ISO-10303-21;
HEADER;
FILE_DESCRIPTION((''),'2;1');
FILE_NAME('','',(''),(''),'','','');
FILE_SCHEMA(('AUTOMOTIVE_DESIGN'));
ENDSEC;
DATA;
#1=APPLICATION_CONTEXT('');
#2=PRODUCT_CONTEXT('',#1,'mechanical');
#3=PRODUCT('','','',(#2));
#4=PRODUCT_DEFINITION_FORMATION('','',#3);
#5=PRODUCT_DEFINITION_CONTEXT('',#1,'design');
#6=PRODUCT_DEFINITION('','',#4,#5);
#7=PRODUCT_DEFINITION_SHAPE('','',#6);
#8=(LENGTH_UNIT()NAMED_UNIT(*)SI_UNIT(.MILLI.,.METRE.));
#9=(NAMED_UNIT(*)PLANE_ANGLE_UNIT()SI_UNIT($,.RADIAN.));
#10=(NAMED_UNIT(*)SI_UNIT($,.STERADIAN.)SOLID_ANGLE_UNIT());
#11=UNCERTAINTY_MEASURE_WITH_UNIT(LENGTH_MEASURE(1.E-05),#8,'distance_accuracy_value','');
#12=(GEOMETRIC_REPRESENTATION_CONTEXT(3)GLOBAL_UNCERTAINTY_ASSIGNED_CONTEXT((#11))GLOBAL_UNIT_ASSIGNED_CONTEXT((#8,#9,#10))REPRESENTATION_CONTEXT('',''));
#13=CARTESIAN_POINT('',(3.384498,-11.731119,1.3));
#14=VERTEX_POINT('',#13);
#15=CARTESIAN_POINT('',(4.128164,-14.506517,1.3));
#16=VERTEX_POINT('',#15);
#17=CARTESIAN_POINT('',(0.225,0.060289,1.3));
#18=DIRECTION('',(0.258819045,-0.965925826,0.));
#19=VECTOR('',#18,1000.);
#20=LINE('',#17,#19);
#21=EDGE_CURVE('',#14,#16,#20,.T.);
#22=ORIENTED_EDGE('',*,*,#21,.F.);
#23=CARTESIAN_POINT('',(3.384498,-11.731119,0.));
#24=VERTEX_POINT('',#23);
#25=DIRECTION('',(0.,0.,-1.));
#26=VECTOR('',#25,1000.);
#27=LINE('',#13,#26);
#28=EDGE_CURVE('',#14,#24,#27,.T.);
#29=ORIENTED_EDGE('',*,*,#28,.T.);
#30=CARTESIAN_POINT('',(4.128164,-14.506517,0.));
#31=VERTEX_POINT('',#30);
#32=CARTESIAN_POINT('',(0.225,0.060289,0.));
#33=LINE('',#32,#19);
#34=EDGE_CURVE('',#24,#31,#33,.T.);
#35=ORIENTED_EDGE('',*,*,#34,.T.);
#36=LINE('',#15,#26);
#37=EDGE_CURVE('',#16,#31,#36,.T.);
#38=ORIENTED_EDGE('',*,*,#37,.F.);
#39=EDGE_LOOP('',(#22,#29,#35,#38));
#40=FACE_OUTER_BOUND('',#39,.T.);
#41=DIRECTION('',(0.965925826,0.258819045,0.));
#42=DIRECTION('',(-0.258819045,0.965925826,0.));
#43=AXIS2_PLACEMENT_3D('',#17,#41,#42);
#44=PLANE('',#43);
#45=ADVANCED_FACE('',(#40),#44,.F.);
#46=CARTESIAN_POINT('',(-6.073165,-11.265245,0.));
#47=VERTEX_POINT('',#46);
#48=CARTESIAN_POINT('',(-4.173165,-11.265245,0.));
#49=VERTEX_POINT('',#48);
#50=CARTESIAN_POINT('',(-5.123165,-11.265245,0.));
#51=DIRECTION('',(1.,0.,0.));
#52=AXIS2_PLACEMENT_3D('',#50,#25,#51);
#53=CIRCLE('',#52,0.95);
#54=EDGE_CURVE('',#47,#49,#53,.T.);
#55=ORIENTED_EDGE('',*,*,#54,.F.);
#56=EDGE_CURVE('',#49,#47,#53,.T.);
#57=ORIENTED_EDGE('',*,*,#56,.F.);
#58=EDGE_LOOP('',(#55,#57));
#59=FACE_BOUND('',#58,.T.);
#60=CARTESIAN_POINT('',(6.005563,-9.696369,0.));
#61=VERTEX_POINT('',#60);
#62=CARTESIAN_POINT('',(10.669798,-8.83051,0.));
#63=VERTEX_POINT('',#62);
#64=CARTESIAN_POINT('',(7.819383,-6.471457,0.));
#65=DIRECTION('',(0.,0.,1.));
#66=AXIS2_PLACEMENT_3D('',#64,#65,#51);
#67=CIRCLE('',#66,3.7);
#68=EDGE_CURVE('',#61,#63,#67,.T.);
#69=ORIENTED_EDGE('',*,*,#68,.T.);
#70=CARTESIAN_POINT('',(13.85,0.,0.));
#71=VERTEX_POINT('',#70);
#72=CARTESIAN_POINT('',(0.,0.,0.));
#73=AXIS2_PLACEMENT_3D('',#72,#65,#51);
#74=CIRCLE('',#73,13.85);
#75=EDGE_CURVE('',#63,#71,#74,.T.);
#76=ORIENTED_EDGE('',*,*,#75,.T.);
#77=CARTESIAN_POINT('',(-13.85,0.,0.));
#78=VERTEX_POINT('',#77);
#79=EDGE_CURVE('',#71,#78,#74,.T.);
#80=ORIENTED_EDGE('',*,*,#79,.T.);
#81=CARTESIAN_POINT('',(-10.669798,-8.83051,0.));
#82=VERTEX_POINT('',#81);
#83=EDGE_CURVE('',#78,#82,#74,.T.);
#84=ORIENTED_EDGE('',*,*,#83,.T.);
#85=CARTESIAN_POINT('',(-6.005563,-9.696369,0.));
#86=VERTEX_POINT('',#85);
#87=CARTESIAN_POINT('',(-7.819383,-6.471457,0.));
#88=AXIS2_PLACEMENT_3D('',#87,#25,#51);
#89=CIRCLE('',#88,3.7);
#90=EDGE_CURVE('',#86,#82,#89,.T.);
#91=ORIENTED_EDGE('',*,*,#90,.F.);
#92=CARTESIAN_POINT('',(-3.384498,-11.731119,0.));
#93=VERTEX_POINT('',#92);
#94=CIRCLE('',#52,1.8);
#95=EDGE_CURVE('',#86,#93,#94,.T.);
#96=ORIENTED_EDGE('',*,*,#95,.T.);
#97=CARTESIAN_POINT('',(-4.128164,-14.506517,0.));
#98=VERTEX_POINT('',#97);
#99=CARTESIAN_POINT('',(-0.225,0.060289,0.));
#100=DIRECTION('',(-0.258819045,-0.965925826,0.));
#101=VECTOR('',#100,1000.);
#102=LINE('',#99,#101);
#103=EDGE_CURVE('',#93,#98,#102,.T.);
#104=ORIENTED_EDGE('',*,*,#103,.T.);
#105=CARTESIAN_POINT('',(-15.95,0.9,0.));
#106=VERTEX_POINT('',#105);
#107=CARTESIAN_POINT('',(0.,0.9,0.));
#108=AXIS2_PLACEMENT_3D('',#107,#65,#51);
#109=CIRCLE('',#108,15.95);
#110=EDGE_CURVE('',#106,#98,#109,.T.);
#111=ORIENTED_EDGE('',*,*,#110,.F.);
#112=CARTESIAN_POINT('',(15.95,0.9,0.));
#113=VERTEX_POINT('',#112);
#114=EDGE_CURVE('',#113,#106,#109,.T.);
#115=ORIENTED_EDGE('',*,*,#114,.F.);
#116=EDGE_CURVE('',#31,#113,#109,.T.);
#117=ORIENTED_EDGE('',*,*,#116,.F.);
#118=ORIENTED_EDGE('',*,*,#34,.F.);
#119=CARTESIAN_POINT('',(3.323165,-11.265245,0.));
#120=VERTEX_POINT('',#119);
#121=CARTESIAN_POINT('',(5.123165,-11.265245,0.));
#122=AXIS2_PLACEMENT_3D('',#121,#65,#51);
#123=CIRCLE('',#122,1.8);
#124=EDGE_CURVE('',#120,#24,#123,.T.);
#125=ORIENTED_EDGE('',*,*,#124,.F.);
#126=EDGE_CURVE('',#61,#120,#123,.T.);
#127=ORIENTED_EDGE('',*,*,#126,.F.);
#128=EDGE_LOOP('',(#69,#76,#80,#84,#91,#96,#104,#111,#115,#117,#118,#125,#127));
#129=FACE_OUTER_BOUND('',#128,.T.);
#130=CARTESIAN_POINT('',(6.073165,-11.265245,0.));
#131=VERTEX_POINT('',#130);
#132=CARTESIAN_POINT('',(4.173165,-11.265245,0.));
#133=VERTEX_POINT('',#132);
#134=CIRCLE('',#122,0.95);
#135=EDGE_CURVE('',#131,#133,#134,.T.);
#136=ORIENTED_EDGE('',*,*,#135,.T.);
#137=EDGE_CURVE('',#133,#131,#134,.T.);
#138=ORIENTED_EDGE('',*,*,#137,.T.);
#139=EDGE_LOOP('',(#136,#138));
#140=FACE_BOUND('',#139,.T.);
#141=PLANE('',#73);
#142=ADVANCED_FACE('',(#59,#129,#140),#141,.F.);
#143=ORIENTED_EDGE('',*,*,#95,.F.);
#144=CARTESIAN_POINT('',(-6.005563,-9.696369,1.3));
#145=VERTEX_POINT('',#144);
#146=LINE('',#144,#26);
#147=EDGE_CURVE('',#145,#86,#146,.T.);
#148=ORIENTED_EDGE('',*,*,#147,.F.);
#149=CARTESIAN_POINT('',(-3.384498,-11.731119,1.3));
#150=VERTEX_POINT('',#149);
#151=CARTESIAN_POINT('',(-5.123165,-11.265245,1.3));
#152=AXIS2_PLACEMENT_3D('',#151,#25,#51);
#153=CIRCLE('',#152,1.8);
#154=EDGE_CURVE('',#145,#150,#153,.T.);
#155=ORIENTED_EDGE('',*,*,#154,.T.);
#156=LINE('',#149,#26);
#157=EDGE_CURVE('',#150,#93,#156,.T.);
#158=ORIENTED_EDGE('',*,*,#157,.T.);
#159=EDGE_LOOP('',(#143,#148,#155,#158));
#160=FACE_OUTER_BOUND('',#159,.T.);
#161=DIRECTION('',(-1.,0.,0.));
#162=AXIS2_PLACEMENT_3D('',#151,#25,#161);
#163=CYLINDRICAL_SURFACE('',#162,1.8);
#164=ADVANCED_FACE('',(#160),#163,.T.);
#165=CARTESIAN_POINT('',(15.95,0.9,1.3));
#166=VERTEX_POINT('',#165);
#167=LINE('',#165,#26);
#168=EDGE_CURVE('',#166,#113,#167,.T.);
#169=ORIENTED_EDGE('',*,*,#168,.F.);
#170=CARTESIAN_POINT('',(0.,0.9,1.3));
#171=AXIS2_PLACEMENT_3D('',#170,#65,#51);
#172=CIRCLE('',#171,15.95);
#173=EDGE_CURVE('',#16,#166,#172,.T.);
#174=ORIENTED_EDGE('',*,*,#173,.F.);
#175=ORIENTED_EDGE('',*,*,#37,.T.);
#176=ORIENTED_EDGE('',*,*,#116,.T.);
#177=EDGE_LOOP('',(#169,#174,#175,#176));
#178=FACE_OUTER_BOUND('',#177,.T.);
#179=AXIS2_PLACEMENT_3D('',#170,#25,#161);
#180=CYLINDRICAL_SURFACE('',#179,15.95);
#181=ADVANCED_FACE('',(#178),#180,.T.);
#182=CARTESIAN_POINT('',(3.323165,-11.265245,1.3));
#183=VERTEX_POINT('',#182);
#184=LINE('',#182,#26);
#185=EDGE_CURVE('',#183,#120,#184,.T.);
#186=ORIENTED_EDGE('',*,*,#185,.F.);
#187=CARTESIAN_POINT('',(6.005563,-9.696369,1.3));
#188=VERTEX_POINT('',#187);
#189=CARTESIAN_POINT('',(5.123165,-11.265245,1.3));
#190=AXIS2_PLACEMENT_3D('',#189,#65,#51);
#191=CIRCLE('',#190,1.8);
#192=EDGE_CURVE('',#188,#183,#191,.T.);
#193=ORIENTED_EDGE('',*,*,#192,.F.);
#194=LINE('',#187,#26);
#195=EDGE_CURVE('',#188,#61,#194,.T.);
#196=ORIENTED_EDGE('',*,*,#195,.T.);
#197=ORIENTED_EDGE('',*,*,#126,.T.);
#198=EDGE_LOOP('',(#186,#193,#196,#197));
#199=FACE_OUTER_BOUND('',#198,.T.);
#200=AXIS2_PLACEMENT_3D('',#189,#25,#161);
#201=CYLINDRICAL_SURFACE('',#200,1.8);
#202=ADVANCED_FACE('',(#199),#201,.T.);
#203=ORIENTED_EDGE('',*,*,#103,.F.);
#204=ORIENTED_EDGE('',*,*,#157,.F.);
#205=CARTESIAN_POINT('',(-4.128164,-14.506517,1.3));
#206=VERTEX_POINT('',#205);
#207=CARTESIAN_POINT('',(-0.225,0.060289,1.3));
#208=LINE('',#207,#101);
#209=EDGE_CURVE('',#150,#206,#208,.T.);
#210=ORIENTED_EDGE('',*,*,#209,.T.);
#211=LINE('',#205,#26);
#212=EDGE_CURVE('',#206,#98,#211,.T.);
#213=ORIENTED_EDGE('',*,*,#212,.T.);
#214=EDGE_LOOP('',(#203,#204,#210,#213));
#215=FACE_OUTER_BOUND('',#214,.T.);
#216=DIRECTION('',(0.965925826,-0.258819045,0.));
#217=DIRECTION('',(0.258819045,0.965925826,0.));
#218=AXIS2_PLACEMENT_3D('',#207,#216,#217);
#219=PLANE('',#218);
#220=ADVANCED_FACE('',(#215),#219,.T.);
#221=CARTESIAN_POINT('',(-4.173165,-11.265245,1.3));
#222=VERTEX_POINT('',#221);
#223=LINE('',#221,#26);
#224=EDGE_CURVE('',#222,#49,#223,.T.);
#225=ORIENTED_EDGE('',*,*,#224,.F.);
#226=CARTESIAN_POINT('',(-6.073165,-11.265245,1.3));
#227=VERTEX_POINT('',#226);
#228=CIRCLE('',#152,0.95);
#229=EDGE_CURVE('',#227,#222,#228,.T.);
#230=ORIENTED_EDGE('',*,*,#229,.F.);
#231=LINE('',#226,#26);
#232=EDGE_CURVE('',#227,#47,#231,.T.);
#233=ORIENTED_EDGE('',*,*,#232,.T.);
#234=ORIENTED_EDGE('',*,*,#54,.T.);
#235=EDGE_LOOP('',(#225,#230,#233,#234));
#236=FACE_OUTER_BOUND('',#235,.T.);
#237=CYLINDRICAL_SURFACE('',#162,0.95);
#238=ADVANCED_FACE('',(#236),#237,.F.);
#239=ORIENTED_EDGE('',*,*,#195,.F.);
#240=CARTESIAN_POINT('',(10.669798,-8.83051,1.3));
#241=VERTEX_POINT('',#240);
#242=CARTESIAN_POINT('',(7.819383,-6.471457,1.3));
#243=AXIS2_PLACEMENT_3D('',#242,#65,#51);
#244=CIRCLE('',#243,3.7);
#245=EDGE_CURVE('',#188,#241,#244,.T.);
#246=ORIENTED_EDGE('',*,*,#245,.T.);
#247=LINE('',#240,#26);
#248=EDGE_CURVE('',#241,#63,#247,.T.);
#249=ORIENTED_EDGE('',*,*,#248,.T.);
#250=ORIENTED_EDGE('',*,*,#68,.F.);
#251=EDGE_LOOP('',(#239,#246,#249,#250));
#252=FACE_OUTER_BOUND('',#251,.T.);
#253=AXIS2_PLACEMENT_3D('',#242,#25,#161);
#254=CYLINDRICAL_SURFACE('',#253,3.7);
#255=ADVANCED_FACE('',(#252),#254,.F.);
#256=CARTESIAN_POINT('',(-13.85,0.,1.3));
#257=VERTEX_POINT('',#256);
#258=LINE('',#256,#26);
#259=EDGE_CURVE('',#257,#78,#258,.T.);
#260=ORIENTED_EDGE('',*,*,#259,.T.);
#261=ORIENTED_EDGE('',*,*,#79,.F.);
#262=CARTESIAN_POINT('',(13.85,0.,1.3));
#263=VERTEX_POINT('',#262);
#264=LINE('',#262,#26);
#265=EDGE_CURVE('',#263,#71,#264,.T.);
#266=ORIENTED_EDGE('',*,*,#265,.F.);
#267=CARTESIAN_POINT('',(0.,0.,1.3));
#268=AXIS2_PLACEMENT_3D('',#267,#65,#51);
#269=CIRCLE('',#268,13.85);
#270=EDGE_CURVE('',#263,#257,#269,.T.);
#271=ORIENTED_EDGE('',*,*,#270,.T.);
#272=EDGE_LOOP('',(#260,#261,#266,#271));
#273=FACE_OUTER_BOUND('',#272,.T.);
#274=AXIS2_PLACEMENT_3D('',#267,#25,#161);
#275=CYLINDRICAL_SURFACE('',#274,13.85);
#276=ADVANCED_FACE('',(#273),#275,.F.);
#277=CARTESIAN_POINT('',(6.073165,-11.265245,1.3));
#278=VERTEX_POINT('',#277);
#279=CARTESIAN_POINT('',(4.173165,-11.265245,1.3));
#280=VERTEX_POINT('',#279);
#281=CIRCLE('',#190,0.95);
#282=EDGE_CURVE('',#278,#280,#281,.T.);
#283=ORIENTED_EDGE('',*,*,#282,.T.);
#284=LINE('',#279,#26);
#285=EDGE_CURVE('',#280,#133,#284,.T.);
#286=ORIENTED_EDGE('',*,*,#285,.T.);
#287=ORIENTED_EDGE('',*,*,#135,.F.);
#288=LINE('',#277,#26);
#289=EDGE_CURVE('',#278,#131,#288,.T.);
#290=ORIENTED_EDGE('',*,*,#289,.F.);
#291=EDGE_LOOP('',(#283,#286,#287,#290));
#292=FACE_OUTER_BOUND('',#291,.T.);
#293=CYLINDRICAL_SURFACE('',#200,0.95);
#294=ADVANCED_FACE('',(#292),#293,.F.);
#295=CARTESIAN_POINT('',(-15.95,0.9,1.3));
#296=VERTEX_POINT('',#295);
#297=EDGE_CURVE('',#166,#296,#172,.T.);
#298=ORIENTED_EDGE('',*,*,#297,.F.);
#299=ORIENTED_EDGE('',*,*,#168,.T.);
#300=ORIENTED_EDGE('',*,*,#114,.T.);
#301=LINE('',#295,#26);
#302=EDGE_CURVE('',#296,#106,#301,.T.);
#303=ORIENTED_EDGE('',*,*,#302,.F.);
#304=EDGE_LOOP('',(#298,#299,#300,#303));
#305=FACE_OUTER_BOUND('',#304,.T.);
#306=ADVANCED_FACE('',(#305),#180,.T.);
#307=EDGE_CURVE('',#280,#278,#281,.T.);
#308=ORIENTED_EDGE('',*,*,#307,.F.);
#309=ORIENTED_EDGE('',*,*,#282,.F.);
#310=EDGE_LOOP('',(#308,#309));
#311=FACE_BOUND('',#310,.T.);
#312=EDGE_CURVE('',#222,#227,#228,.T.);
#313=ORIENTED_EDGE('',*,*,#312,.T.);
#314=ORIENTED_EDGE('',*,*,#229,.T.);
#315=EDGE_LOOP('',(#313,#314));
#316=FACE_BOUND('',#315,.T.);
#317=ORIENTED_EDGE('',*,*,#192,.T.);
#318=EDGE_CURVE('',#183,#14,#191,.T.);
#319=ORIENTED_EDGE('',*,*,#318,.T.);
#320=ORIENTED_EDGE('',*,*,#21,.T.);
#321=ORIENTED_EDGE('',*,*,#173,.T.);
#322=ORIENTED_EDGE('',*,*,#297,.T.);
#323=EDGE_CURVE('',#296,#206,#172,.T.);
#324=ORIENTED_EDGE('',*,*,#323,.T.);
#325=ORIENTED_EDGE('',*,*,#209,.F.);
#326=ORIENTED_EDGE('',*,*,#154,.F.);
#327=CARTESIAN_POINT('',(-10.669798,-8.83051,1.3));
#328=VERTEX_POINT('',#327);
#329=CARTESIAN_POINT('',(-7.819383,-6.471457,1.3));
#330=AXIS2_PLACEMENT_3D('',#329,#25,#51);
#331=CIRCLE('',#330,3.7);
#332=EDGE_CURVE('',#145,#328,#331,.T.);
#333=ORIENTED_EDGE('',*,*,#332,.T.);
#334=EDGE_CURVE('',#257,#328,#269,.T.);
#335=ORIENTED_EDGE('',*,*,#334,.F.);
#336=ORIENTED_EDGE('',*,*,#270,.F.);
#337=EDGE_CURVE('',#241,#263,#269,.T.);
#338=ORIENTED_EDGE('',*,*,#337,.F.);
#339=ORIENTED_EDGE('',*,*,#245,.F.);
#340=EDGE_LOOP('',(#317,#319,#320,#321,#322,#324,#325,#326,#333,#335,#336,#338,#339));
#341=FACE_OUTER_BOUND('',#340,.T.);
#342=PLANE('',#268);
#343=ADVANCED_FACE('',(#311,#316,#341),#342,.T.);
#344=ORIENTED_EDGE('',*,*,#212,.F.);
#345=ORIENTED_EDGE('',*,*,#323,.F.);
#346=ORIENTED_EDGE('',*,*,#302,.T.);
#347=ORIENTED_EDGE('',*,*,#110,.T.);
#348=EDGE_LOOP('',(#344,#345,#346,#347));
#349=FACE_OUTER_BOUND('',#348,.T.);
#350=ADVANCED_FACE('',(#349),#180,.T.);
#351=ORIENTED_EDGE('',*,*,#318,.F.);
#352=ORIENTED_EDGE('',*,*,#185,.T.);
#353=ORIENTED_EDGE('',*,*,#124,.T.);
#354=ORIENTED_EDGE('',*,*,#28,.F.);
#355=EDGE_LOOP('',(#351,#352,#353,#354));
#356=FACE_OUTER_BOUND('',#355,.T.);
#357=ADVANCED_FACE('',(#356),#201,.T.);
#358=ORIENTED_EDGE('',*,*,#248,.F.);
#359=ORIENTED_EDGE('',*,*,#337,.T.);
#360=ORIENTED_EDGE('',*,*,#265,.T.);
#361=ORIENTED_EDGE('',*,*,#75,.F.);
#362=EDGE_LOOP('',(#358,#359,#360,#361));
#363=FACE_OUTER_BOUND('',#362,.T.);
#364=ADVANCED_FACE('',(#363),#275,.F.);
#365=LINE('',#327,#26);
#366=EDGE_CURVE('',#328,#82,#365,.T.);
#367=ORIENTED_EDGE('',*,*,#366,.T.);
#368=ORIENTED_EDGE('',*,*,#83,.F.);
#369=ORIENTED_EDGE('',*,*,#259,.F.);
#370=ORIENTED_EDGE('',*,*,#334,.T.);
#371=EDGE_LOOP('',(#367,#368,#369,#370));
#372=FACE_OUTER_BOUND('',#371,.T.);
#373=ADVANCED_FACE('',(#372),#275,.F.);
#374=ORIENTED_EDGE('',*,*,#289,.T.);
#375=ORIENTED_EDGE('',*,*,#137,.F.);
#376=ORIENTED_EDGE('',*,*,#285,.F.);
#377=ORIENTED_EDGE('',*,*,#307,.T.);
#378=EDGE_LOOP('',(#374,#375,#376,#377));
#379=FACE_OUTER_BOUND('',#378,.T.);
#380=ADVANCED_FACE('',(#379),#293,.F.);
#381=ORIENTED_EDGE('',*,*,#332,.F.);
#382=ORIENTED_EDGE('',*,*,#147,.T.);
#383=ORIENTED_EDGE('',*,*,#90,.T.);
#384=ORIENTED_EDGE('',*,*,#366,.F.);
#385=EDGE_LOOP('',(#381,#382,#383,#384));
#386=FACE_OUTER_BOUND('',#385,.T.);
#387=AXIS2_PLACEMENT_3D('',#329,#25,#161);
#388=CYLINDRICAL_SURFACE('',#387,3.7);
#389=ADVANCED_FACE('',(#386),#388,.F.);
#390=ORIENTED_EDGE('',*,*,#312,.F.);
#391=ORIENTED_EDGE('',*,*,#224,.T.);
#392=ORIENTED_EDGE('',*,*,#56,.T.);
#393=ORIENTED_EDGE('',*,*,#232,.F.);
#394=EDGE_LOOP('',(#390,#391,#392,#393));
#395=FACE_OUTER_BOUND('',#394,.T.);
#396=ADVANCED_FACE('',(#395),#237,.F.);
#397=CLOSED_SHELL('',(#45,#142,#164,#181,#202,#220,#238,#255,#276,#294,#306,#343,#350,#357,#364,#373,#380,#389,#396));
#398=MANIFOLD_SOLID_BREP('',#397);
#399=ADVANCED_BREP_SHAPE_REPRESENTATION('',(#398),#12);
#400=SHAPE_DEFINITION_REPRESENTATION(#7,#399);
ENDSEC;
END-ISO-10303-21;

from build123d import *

# Parameters (mm, degrees)
SKETCH1_R           = 0.95
BOSS_EXTRUDE1_DEPTH = 1.3


with BuildPart() as part:
    # Sketch1 → Boss-Extrude1 (new body)
    with BuildSketch(Plane.XY):
        with BuildLine():
            ThreePointArc((-6.005563392, -9.696368719), (-4.019375294, -9.84339787), (-3.384498187, -11.731119191))
            Line((-3.384498187, -11.731119191), (-4.128163769, -14.506516929))
            ThreePointArc((-4.128163769, -14.506516929), (0, 16.85), (4.128163769, -14.506516929))
            Line((4.128163769, -14.506516929), (3.384498187, -11.731119191))
            ThreePointArc((3.384498187, -11.731119191), (4.019375294, -9.84339787), (6.005563392, -9.696368719))
            ThreePointArc((6.005563392, -9.696368719), (8.494705662, -10.109304713), (10.669798447, -8.830509674))
            ThreePointArc((10.669798447, -8.830509674), (0, 13.85), (-10.669798447, -8.830509674))
            ThreePointArc((-10.669798447, -8.830509674), (-8.494705662, -10.109304713), (-6.005563392, -9.696368719))
        make_face()
        with Locations((5.123164674, -11.26524491)):
            Circle(SKETCH1_R, mode=Mode.SUBTRACT)
        with Locations((-5.123164674, -11.26524491)):
            Circle(SKETCH1_R, mode=Mode.SUBTRACT)
    extrude(amount=BOSS_EXTRUDE1_DEPTH)


solid = part.part
